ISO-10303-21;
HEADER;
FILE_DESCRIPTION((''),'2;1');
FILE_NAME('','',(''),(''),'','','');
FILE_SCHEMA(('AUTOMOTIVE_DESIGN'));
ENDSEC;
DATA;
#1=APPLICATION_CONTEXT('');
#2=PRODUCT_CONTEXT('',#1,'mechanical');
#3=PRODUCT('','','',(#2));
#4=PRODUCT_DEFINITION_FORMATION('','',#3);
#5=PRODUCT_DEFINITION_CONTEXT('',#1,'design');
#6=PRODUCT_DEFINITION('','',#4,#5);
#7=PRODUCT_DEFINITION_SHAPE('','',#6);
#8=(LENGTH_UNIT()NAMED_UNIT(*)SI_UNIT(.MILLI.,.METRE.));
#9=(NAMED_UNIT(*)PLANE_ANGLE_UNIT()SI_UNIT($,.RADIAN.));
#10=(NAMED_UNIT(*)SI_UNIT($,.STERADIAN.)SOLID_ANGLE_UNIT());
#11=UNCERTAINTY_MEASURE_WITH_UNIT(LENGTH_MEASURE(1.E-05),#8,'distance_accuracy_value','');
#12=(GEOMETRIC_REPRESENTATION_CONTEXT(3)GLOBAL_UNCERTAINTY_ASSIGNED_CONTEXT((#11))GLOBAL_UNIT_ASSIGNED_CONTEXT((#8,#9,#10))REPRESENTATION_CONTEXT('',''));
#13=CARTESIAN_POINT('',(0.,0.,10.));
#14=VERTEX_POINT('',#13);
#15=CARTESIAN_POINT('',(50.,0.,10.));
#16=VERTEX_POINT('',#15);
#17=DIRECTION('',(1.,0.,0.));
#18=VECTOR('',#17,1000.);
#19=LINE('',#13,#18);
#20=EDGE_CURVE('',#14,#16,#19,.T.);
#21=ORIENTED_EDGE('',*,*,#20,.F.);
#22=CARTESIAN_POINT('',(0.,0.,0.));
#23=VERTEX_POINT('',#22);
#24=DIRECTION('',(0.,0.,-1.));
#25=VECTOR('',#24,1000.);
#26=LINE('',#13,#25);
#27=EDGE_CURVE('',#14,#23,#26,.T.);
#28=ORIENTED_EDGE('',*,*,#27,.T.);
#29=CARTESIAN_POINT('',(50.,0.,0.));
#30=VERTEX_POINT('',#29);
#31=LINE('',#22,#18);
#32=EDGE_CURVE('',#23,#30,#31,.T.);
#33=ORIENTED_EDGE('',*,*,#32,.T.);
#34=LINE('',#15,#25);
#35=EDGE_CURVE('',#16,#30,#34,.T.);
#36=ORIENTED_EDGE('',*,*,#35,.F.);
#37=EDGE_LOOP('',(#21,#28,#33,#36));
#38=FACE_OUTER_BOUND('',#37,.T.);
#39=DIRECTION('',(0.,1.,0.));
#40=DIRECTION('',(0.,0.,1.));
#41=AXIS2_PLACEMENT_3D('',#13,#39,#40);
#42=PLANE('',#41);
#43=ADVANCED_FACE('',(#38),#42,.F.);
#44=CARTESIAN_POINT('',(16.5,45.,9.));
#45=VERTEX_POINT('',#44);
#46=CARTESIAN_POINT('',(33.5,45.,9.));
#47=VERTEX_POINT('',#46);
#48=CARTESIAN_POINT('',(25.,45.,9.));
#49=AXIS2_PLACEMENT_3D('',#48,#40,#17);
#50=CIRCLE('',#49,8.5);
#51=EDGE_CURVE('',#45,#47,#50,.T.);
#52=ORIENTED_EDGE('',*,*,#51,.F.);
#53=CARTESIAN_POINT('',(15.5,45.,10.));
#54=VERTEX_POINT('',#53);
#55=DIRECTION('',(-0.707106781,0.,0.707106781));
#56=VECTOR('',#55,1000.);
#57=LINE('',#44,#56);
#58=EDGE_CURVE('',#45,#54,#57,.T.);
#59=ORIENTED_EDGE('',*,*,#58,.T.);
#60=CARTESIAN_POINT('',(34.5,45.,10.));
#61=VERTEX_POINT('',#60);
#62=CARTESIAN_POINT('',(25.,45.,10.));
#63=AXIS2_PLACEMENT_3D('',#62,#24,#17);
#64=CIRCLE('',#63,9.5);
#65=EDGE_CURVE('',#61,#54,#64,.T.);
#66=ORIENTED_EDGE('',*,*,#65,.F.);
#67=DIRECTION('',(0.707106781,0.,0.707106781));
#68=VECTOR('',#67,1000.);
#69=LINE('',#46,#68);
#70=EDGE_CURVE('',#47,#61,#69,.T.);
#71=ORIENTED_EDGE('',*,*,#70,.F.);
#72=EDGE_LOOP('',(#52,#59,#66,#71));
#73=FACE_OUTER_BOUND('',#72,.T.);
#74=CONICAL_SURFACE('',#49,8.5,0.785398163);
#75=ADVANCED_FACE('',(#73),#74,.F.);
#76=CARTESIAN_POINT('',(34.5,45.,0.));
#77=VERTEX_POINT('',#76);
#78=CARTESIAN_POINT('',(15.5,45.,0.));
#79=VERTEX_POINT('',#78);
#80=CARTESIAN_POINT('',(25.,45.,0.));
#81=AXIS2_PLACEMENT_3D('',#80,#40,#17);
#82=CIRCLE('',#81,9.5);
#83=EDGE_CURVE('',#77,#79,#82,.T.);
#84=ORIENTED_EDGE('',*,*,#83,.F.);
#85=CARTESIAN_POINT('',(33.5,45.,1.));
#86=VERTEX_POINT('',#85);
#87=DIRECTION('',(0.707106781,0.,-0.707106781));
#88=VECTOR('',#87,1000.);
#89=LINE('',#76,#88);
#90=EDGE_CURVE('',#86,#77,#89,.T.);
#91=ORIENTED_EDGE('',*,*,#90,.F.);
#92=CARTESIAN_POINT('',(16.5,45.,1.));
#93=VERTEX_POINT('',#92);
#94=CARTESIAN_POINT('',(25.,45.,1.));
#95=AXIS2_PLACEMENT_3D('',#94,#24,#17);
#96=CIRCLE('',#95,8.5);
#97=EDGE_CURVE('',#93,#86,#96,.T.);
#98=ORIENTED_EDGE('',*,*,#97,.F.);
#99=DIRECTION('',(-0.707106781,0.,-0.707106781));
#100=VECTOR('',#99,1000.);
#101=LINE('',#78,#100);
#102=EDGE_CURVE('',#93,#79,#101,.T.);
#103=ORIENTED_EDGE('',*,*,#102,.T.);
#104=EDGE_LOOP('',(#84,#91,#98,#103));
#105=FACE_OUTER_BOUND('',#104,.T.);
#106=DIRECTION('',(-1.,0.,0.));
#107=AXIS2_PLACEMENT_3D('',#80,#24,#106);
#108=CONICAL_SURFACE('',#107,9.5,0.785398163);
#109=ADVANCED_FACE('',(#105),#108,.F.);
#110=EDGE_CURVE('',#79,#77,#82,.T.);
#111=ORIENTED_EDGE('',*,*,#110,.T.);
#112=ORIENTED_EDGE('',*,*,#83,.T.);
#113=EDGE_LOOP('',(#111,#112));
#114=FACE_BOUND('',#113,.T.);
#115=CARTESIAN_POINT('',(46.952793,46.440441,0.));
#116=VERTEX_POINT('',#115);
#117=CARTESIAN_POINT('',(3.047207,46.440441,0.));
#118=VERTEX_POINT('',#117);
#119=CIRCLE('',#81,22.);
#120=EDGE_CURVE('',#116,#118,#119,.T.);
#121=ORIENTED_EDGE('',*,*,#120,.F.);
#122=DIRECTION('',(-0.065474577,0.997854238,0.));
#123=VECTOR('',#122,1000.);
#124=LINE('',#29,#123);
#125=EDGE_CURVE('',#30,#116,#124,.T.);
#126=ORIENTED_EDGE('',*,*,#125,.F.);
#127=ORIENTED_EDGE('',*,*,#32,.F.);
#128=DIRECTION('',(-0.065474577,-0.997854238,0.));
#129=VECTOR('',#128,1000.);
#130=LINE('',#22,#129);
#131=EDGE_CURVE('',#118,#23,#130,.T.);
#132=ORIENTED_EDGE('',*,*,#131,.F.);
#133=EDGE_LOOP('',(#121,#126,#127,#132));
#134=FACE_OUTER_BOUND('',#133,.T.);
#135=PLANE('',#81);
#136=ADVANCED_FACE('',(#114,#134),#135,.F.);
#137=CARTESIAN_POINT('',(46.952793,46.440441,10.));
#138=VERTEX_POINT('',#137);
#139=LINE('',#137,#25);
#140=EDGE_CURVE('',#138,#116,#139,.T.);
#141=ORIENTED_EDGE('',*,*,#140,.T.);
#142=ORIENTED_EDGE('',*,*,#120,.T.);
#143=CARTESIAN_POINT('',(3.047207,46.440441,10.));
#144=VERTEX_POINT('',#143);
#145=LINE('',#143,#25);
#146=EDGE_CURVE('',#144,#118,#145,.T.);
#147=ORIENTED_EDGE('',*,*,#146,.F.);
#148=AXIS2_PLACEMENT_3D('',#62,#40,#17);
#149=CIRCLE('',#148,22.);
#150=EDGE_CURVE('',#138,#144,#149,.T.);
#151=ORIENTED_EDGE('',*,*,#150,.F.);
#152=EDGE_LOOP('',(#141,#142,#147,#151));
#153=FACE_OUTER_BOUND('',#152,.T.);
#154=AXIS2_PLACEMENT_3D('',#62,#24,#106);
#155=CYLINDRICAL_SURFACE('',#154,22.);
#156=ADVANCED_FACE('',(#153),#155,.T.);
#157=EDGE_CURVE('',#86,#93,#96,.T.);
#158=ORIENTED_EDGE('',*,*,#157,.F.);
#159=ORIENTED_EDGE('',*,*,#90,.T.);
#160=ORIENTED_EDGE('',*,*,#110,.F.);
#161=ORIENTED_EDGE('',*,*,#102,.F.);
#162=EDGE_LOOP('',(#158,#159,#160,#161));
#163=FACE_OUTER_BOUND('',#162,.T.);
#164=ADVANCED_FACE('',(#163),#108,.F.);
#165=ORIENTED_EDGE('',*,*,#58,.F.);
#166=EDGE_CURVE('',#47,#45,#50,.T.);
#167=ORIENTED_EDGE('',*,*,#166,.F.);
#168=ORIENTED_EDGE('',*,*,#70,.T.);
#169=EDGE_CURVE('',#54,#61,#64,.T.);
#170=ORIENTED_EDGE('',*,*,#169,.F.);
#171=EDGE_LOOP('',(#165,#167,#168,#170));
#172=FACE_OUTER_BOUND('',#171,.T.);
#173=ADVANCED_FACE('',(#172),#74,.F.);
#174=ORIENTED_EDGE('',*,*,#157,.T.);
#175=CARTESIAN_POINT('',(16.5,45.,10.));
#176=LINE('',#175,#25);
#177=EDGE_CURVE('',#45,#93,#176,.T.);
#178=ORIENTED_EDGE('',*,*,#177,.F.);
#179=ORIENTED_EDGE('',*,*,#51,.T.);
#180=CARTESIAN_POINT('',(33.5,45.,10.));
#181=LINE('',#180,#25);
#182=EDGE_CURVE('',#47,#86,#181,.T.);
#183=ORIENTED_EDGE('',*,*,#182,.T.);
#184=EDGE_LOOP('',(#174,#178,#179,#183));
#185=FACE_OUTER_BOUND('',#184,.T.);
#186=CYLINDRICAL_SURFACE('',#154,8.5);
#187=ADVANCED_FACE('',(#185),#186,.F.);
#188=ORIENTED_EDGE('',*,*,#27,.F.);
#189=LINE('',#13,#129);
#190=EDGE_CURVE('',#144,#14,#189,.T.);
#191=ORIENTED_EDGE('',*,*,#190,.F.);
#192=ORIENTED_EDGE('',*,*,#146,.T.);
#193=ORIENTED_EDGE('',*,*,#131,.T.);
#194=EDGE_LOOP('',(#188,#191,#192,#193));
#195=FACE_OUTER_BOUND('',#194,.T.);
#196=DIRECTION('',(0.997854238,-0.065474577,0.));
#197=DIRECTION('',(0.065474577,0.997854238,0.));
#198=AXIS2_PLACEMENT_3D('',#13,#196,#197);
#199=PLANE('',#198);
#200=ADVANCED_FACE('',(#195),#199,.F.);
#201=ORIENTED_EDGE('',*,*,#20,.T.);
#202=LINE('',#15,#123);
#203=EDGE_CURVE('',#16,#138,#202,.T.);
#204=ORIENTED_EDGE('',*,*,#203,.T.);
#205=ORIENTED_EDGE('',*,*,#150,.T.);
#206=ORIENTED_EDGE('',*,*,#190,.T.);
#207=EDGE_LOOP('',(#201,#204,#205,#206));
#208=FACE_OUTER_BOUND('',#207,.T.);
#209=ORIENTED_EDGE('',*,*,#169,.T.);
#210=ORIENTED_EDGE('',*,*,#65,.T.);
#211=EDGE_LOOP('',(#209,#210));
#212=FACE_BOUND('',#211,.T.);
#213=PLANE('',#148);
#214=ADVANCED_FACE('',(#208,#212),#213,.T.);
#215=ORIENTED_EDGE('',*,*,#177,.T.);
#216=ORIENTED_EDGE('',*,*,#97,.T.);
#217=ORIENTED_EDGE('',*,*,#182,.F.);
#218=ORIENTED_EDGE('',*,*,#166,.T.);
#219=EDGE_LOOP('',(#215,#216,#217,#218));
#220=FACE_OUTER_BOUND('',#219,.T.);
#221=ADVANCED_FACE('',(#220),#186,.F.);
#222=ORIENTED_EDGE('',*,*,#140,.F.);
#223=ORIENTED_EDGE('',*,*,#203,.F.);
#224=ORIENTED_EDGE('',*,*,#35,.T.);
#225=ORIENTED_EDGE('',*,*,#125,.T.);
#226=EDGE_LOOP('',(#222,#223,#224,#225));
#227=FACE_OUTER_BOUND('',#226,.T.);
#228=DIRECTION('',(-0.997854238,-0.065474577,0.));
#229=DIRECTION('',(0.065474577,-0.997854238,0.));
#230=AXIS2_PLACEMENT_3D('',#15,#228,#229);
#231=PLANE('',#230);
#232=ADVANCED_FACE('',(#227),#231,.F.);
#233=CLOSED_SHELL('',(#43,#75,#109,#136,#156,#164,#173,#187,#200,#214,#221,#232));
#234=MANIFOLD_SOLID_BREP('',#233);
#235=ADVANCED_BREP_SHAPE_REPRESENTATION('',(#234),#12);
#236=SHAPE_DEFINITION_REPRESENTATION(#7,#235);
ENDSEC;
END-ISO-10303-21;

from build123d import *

# Parameters (mm, degrees)
SKETCH1_R           = 8.5
BOSS_EXTRUDE1_DEPTH = 10
CHAMFER1_SIZE       = 1


with BuildPart() as part:
    # Sketch1 → Boss-Extrude1 (new body)
    with BuildSketch(Plane.XY):
        with BuildLine():
            Line((0, 0), (50, 0))
            Line((50, 0), (46.952793231, 46.440440684))
            ThreePointArc((46.952793231, 46.440440684), (25, 67), (3.047206769, 46.440440684))
            Line((3.047206769, 46.440440684), (0, 0))
        make_face()
        with Locations((25, 45)):
            Circle(SKETCH1_R, mode=Mode.SUBTRACT)
    extrude(amount=BOSS_EXTRUDE1_DEPTH)

    # Chamfer1
    chamfer1_edges = [part.edges().sort_by_distance(p)[0] for p in [
        (16.5, 45, 0),
        (16.5, 45, 10),
    ]]
    chamfer(chamfer1_edges, length=CHAMFER1_SIZE)


solid = part.part
